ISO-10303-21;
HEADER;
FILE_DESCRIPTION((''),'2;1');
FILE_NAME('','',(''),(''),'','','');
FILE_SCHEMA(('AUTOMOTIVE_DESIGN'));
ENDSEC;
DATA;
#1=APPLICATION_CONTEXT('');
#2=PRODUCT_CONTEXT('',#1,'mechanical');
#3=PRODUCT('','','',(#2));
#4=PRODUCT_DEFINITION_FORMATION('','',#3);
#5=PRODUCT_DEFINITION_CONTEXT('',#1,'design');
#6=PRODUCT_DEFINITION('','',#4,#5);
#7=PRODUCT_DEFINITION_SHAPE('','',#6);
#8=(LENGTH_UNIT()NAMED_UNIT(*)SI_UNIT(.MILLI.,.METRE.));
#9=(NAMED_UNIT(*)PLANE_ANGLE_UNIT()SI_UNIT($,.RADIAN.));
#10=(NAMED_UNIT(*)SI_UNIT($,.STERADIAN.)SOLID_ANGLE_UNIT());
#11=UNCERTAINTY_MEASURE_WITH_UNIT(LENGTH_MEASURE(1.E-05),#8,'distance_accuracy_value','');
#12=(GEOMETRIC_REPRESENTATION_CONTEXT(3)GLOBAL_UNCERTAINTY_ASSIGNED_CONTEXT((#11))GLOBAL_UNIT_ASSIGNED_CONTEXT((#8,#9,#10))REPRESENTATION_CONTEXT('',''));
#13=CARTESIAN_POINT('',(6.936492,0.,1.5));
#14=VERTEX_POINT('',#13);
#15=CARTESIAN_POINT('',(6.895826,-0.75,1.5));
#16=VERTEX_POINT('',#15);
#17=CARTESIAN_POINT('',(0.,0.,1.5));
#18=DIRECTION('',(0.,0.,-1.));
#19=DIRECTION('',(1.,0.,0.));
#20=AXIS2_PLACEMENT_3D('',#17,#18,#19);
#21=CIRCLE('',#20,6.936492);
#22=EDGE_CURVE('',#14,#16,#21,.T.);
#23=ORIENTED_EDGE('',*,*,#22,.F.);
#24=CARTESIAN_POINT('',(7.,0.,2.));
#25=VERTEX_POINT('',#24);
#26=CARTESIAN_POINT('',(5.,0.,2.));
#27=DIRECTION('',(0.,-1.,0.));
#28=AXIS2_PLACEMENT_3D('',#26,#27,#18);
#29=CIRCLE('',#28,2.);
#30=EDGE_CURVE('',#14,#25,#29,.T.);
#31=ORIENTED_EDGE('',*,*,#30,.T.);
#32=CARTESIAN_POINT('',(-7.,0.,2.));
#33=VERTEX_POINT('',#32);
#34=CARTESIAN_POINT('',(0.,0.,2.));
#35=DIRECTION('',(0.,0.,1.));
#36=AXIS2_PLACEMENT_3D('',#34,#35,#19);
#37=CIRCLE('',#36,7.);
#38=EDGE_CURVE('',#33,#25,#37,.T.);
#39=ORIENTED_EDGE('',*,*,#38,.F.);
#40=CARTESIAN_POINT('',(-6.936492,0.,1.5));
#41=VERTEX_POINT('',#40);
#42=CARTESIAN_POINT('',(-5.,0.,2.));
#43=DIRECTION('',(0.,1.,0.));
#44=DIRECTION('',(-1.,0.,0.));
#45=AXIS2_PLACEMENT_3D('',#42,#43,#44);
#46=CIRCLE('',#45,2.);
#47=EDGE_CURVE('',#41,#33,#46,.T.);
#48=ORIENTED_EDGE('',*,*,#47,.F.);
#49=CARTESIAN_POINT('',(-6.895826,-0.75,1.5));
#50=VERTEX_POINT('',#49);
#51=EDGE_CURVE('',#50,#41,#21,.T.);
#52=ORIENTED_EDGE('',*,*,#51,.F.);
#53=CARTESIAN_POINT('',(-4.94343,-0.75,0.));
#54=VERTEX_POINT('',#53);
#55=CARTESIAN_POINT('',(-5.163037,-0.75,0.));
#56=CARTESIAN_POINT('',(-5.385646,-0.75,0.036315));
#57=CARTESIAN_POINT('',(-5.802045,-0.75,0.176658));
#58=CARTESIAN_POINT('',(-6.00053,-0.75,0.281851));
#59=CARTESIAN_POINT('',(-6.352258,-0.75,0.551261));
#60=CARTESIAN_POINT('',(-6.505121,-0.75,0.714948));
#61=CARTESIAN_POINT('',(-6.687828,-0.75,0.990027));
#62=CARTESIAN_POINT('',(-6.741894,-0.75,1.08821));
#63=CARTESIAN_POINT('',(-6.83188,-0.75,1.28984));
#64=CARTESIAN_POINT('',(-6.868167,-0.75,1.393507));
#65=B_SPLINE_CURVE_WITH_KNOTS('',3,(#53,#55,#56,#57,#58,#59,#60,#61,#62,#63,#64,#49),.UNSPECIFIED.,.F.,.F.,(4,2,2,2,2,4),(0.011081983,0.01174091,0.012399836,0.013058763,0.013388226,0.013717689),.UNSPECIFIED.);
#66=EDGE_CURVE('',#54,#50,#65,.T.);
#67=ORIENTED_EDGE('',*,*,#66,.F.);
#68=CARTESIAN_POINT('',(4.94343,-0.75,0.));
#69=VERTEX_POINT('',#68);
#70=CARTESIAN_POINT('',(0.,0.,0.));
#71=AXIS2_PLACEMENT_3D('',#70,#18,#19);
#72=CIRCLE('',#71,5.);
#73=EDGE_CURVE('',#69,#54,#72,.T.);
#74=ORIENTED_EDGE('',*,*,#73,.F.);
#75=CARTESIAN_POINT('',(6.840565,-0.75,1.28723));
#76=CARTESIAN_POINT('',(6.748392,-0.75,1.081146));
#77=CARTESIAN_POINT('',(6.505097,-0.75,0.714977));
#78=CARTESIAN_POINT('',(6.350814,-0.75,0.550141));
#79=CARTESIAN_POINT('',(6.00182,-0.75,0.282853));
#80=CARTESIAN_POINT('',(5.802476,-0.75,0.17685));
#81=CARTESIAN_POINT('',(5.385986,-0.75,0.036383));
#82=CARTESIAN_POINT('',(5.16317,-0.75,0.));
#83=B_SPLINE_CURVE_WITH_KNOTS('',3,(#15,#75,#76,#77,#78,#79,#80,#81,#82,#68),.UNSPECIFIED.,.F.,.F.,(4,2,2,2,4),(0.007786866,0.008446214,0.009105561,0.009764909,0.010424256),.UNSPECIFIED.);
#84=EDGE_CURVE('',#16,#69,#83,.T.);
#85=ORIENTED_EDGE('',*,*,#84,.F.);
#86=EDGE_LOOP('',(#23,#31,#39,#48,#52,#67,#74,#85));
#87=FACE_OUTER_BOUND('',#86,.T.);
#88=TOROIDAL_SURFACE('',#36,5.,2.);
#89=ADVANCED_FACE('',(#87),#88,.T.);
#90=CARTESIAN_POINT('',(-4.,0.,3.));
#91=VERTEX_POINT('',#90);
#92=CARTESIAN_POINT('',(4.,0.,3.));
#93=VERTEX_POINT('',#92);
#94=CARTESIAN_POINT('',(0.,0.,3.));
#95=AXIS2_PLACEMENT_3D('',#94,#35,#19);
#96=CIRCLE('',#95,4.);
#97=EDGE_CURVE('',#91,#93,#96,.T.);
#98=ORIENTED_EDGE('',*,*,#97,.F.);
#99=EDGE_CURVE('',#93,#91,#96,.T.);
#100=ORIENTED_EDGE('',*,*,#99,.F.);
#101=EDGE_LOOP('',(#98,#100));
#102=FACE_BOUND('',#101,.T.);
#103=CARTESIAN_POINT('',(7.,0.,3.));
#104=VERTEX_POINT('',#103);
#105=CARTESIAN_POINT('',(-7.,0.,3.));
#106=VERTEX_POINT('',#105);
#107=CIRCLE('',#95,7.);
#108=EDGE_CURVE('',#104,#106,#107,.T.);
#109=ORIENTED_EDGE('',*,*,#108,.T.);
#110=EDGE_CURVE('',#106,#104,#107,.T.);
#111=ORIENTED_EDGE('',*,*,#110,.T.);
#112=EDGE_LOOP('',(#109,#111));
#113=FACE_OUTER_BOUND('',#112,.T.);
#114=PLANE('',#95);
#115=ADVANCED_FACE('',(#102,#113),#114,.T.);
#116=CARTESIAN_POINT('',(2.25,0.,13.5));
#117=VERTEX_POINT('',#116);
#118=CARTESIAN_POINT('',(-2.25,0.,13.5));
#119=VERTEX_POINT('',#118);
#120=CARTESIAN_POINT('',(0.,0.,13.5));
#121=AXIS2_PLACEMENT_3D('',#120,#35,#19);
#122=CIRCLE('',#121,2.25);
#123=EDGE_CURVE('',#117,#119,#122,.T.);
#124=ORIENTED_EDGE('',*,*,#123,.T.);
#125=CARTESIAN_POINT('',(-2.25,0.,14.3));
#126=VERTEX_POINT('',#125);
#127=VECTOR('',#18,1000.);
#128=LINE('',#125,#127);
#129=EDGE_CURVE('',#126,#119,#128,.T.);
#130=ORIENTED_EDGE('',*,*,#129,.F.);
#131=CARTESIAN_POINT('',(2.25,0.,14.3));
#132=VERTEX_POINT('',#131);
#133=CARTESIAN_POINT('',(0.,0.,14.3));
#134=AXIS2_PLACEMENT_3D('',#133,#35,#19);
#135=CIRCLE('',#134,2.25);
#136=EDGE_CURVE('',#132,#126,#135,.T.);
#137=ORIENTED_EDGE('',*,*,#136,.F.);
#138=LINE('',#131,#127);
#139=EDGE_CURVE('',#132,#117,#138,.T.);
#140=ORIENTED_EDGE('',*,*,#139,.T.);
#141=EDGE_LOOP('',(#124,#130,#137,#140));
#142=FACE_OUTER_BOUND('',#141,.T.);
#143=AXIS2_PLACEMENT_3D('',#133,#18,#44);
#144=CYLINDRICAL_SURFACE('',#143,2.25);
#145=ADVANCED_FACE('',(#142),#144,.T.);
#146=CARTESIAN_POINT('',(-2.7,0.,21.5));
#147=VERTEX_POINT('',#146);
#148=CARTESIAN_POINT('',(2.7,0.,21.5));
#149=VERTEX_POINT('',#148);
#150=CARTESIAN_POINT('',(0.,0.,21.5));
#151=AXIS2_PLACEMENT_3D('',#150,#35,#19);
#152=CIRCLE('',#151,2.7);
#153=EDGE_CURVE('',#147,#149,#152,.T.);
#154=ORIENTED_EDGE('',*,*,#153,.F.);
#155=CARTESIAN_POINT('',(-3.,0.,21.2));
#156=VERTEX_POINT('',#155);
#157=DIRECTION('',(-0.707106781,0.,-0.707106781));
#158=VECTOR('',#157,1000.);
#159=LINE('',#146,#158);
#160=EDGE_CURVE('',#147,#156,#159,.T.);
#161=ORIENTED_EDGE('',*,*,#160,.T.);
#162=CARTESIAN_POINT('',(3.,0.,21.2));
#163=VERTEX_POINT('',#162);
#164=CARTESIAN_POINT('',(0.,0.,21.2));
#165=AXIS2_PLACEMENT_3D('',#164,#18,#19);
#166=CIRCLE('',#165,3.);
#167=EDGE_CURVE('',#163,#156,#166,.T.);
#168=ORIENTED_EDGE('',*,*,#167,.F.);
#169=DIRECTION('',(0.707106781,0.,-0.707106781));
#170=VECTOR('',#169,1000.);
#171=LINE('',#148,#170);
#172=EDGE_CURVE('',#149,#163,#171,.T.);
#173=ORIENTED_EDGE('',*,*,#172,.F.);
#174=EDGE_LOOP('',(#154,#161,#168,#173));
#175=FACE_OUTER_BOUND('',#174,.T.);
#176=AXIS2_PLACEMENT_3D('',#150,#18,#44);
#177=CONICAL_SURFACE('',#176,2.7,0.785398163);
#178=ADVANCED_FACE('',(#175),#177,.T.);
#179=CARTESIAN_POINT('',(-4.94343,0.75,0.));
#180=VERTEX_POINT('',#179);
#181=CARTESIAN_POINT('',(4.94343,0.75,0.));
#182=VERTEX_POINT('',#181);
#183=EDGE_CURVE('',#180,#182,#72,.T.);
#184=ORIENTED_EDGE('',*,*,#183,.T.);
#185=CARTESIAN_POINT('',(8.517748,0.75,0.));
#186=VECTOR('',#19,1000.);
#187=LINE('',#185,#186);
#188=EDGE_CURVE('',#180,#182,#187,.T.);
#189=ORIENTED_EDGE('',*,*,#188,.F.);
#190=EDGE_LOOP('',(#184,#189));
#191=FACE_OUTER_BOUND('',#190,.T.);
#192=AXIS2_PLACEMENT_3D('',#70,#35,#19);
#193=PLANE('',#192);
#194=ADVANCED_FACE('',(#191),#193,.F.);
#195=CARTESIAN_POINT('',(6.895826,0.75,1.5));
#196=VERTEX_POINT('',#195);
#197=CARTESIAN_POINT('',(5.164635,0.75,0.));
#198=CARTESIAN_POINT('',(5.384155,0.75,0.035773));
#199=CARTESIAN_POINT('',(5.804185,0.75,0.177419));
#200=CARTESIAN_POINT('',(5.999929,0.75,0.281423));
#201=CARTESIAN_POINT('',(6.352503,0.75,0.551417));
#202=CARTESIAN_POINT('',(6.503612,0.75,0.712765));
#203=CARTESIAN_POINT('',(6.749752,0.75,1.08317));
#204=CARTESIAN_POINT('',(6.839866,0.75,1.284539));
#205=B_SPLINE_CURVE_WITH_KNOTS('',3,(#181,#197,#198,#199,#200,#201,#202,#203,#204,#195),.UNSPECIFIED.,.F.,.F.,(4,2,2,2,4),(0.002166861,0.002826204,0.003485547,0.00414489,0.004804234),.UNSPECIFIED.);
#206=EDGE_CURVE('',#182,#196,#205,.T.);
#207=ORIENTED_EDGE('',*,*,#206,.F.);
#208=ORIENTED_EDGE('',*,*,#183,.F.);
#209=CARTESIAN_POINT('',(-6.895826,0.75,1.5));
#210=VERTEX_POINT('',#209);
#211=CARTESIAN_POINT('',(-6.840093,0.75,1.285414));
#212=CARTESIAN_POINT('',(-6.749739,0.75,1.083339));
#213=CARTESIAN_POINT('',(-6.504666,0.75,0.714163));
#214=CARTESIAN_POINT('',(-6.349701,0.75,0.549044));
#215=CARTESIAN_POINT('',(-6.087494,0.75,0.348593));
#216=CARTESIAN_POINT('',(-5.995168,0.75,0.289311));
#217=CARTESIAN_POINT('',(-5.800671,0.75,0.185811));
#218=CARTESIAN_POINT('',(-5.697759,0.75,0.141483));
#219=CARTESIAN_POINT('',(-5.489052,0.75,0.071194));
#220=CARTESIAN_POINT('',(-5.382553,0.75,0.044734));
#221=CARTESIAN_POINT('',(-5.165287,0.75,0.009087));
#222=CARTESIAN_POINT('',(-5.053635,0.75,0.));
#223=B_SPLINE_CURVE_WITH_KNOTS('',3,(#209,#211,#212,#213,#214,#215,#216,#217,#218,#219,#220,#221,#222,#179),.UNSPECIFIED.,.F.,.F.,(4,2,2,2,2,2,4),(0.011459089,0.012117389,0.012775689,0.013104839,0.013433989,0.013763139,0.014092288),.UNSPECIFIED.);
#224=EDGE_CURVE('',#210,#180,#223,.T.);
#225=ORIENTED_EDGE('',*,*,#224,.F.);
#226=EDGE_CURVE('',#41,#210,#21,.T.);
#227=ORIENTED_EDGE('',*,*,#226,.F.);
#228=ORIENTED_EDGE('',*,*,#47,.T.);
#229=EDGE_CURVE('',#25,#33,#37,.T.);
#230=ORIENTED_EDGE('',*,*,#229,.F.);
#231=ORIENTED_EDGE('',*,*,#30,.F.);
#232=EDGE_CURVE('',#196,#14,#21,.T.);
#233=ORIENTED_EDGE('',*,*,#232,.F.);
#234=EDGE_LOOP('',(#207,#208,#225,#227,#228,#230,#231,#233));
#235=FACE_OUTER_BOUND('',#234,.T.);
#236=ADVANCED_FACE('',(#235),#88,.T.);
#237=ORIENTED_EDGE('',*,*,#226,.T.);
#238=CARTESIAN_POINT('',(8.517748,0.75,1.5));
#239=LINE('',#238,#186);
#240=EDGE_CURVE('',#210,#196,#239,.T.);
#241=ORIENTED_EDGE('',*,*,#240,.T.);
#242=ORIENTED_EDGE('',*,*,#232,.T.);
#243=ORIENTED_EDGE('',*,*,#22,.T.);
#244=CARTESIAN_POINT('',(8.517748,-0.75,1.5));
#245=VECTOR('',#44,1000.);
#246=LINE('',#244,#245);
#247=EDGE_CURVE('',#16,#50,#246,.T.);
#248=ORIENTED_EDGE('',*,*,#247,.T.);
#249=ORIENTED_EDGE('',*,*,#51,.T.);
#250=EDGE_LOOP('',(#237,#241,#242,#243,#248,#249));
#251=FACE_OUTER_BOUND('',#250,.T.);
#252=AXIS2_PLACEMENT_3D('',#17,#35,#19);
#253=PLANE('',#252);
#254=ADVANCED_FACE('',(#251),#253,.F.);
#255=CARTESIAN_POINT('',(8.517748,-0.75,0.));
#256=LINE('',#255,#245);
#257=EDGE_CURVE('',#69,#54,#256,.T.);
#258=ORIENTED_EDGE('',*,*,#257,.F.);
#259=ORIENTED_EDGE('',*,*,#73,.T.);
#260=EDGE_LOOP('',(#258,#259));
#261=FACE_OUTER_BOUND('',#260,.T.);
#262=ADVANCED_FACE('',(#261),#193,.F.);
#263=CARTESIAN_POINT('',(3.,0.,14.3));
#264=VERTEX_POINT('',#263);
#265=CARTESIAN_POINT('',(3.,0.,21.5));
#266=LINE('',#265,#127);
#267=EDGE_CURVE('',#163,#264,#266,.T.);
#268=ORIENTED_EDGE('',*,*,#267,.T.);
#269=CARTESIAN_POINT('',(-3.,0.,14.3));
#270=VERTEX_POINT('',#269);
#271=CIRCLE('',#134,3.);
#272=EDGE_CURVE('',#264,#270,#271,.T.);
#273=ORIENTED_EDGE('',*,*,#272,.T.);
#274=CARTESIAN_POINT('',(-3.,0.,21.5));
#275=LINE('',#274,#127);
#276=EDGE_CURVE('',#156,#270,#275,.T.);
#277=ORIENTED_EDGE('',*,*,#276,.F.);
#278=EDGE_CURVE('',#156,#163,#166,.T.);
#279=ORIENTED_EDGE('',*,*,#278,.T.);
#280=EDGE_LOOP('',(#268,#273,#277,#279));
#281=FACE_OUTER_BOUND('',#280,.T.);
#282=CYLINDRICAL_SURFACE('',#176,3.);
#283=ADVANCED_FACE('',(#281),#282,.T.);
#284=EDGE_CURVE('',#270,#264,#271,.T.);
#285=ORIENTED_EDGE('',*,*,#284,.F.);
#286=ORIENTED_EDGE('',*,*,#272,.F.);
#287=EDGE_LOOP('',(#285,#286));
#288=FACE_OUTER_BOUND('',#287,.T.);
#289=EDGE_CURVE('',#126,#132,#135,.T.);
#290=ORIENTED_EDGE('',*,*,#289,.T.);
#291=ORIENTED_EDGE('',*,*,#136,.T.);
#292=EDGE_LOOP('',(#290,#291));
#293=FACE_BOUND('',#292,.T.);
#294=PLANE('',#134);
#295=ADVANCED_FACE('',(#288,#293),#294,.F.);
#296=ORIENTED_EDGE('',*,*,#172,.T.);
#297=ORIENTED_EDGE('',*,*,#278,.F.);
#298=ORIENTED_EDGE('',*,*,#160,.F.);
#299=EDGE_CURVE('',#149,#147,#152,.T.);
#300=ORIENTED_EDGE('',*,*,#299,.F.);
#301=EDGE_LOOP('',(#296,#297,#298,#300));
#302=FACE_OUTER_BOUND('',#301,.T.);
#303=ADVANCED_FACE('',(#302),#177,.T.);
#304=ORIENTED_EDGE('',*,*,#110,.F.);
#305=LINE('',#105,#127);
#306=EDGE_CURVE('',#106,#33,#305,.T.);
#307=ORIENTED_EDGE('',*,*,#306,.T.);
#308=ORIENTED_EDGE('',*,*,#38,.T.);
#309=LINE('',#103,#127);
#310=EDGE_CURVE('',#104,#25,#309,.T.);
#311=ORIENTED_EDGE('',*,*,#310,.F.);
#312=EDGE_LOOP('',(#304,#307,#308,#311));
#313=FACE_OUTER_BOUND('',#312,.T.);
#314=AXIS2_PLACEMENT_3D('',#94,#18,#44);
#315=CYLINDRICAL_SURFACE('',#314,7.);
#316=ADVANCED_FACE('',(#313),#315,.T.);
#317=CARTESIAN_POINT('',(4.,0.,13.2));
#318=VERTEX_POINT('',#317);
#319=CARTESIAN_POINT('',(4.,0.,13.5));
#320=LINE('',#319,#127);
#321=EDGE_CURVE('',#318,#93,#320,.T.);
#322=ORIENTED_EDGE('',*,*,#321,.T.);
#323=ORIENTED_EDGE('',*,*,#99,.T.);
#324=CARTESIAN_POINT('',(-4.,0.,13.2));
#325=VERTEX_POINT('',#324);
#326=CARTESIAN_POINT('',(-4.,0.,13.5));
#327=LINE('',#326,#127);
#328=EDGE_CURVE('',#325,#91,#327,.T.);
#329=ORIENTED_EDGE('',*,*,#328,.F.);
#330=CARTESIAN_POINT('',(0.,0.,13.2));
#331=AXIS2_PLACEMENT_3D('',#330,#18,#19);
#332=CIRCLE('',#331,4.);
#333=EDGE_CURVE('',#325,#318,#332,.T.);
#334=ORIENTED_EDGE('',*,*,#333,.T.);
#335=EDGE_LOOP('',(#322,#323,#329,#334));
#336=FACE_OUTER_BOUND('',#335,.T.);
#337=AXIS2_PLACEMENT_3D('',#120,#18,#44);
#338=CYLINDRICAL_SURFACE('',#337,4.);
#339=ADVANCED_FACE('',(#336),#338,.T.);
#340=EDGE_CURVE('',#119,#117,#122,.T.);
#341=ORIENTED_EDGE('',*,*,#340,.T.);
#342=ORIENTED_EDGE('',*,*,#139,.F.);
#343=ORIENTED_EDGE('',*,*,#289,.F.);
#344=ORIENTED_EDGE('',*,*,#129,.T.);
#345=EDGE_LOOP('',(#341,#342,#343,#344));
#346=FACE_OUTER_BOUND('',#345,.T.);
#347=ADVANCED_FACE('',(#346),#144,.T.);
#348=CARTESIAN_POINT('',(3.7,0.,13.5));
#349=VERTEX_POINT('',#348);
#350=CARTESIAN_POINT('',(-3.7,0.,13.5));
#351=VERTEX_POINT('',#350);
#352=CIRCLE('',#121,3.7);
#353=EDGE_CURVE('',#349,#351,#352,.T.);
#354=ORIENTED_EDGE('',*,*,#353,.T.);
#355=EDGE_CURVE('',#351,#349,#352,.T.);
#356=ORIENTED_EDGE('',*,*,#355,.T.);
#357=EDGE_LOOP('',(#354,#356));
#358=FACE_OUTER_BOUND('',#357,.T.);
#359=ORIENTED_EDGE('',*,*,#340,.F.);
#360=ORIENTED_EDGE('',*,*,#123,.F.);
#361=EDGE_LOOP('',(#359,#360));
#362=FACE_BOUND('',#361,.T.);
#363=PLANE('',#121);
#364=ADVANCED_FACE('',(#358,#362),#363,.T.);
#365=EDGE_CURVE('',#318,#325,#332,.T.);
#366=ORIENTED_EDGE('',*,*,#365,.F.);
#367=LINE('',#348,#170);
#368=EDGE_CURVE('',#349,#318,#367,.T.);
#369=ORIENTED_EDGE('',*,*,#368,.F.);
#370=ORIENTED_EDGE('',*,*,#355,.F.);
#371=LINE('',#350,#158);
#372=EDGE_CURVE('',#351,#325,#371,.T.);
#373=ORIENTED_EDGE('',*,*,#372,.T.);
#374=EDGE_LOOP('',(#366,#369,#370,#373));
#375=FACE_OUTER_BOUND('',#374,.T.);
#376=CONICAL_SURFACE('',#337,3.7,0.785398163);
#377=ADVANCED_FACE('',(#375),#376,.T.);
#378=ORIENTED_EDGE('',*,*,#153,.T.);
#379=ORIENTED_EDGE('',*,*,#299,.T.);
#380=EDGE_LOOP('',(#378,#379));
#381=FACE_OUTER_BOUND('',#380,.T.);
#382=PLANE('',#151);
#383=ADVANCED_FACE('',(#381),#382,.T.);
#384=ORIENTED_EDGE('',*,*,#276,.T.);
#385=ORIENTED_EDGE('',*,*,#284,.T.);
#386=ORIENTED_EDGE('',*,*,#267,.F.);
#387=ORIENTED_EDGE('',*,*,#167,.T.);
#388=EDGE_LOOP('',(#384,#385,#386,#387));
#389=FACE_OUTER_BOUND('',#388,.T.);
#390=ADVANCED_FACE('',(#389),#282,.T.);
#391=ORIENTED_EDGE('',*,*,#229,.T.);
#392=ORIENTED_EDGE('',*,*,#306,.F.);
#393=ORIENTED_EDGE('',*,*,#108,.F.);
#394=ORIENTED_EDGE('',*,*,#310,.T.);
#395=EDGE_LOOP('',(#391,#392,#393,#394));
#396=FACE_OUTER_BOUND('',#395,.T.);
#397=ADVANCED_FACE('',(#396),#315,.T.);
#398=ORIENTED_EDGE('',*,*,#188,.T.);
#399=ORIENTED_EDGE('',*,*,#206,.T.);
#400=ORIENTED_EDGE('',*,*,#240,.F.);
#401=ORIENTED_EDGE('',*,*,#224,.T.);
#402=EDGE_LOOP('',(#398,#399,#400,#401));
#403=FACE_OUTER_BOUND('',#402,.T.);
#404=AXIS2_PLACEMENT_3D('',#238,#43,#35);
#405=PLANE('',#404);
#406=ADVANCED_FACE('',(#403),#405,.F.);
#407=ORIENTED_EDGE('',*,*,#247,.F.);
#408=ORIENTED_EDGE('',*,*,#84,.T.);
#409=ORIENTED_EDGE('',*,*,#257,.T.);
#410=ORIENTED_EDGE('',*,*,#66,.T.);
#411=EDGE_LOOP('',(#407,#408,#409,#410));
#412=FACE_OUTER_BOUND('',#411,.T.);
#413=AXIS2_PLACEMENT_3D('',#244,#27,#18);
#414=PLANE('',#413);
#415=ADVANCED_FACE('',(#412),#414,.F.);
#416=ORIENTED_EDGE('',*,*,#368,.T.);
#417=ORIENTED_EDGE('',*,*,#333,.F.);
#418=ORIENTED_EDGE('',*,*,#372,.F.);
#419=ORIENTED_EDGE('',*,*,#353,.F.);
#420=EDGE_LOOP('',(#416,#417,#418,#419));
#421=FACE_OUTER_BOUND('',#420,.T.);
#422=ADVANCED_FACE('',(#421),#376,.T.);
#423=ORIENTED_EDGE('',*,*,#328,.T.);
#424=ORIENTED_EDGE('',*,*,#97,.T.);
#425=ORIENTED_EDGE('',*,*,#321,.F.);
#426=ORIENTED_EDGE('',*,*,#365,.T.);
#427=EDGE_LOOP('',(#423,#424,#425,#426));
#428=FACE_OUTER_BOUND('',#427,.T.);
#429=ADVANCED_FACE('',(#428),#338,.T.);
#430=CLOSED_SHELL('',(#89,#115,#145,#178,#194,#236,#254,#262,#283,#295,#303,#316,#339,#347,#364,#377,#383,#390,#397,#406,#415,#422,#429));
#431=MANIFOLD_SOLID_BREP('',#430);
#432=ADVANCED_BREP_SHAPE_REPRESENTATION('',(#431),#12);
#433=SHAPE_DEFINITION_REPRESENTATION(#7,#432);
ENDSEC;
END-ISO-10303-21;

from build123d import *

# Parameters (mm, degrees)
SKETCH_1_R          = 7
EXTRUDE_1_DEPTH     = 3
SKETCH_2_R          = 4
EXTRUDE_2_DEPTH     = 10.5
SKETCH_3_R          = 3
EXTRUDE_3_DEPTH     = 8
SKETCH_4_R          = 3
SKETCH_4_R_2        = 2.25
CUT_EXTRUDE_1_DEPTH = 0.8
FILLET_1_R          = 2
SKETCH_5_W          = 17.035496118
SKETCH_5_H          = 1.5
CUT_EXTRUDE_2_DEPTH = 1.5
CHAMFER_1_SIZE      = 0.3


with BuildPart() as part:
    # 草图1 → 凸台-拉伸1 (new body)
    with BuildSketch(Plane.XY):
        Circle(SKETCH_1_R)
    extrude(amount=EXTRUDE_1_DEPTH)

    # 草图2 → 凸台-拉伸2 (add)
    with BuildSketch(Plane.XY.offset(3)):
        with Locations(Location((0, 0, 0), (0, 0, 180))):
            Circle(SKETCH_2_R)
    extrude(amount=EXTRUDE_2_DEPTH)

    # 草图3 → 凸台-拉伸3 (add)
    with BuildSketch(Plane.XY.offset(13.5)):
        Circle(SKETCH_3_R)
    extrude(amount=EXTRUDE_3_DEPTH)

    # 草图4 → 切除-拉伸1 (cut)
    with BuildSketch(Plane.XY.offset(13.5)):
        Circle(SKETCH_4_R)
        Circle(SKETCH_4_R_2, mode=Mode.SUBTRACT)
    extrude(amount=CUT_EXTRUDE_1_DEPTH, mode=Mode.SUBTRACT)

    # 圆角1
    fillet_1_edges = [part.edges().sort_by_distance(p)[0] for p in [
        (-7, 0, 0),
    ]]
    fillet(fillet_1_edges, radius=FILLET_1_R)

    # 草图5 → 切除-拉伸2 (cut)
    with BuildSketch(Plane(origin=(0, 0, 0), x_dir=(-1, 0, 0), z_dir=(0, 0, -1))):
        Rectangle(SKETCH_5_W, SKETCH_5_H)
    extrude(amount=-CUT_EXTRUDE_2_DEPTH, mode=Mode.SUBTRACT)

    # 倒角1
    chamfer_1_edges = [part.edges().sort_by_distance(p)[0] for p in [
        (-3, 0, 21.5),
        (4, 0, 13.5),
    ]]
    chamfer(chamfer_1_edges, length=CHAMFER_1_SIZE)


solid = part.part
